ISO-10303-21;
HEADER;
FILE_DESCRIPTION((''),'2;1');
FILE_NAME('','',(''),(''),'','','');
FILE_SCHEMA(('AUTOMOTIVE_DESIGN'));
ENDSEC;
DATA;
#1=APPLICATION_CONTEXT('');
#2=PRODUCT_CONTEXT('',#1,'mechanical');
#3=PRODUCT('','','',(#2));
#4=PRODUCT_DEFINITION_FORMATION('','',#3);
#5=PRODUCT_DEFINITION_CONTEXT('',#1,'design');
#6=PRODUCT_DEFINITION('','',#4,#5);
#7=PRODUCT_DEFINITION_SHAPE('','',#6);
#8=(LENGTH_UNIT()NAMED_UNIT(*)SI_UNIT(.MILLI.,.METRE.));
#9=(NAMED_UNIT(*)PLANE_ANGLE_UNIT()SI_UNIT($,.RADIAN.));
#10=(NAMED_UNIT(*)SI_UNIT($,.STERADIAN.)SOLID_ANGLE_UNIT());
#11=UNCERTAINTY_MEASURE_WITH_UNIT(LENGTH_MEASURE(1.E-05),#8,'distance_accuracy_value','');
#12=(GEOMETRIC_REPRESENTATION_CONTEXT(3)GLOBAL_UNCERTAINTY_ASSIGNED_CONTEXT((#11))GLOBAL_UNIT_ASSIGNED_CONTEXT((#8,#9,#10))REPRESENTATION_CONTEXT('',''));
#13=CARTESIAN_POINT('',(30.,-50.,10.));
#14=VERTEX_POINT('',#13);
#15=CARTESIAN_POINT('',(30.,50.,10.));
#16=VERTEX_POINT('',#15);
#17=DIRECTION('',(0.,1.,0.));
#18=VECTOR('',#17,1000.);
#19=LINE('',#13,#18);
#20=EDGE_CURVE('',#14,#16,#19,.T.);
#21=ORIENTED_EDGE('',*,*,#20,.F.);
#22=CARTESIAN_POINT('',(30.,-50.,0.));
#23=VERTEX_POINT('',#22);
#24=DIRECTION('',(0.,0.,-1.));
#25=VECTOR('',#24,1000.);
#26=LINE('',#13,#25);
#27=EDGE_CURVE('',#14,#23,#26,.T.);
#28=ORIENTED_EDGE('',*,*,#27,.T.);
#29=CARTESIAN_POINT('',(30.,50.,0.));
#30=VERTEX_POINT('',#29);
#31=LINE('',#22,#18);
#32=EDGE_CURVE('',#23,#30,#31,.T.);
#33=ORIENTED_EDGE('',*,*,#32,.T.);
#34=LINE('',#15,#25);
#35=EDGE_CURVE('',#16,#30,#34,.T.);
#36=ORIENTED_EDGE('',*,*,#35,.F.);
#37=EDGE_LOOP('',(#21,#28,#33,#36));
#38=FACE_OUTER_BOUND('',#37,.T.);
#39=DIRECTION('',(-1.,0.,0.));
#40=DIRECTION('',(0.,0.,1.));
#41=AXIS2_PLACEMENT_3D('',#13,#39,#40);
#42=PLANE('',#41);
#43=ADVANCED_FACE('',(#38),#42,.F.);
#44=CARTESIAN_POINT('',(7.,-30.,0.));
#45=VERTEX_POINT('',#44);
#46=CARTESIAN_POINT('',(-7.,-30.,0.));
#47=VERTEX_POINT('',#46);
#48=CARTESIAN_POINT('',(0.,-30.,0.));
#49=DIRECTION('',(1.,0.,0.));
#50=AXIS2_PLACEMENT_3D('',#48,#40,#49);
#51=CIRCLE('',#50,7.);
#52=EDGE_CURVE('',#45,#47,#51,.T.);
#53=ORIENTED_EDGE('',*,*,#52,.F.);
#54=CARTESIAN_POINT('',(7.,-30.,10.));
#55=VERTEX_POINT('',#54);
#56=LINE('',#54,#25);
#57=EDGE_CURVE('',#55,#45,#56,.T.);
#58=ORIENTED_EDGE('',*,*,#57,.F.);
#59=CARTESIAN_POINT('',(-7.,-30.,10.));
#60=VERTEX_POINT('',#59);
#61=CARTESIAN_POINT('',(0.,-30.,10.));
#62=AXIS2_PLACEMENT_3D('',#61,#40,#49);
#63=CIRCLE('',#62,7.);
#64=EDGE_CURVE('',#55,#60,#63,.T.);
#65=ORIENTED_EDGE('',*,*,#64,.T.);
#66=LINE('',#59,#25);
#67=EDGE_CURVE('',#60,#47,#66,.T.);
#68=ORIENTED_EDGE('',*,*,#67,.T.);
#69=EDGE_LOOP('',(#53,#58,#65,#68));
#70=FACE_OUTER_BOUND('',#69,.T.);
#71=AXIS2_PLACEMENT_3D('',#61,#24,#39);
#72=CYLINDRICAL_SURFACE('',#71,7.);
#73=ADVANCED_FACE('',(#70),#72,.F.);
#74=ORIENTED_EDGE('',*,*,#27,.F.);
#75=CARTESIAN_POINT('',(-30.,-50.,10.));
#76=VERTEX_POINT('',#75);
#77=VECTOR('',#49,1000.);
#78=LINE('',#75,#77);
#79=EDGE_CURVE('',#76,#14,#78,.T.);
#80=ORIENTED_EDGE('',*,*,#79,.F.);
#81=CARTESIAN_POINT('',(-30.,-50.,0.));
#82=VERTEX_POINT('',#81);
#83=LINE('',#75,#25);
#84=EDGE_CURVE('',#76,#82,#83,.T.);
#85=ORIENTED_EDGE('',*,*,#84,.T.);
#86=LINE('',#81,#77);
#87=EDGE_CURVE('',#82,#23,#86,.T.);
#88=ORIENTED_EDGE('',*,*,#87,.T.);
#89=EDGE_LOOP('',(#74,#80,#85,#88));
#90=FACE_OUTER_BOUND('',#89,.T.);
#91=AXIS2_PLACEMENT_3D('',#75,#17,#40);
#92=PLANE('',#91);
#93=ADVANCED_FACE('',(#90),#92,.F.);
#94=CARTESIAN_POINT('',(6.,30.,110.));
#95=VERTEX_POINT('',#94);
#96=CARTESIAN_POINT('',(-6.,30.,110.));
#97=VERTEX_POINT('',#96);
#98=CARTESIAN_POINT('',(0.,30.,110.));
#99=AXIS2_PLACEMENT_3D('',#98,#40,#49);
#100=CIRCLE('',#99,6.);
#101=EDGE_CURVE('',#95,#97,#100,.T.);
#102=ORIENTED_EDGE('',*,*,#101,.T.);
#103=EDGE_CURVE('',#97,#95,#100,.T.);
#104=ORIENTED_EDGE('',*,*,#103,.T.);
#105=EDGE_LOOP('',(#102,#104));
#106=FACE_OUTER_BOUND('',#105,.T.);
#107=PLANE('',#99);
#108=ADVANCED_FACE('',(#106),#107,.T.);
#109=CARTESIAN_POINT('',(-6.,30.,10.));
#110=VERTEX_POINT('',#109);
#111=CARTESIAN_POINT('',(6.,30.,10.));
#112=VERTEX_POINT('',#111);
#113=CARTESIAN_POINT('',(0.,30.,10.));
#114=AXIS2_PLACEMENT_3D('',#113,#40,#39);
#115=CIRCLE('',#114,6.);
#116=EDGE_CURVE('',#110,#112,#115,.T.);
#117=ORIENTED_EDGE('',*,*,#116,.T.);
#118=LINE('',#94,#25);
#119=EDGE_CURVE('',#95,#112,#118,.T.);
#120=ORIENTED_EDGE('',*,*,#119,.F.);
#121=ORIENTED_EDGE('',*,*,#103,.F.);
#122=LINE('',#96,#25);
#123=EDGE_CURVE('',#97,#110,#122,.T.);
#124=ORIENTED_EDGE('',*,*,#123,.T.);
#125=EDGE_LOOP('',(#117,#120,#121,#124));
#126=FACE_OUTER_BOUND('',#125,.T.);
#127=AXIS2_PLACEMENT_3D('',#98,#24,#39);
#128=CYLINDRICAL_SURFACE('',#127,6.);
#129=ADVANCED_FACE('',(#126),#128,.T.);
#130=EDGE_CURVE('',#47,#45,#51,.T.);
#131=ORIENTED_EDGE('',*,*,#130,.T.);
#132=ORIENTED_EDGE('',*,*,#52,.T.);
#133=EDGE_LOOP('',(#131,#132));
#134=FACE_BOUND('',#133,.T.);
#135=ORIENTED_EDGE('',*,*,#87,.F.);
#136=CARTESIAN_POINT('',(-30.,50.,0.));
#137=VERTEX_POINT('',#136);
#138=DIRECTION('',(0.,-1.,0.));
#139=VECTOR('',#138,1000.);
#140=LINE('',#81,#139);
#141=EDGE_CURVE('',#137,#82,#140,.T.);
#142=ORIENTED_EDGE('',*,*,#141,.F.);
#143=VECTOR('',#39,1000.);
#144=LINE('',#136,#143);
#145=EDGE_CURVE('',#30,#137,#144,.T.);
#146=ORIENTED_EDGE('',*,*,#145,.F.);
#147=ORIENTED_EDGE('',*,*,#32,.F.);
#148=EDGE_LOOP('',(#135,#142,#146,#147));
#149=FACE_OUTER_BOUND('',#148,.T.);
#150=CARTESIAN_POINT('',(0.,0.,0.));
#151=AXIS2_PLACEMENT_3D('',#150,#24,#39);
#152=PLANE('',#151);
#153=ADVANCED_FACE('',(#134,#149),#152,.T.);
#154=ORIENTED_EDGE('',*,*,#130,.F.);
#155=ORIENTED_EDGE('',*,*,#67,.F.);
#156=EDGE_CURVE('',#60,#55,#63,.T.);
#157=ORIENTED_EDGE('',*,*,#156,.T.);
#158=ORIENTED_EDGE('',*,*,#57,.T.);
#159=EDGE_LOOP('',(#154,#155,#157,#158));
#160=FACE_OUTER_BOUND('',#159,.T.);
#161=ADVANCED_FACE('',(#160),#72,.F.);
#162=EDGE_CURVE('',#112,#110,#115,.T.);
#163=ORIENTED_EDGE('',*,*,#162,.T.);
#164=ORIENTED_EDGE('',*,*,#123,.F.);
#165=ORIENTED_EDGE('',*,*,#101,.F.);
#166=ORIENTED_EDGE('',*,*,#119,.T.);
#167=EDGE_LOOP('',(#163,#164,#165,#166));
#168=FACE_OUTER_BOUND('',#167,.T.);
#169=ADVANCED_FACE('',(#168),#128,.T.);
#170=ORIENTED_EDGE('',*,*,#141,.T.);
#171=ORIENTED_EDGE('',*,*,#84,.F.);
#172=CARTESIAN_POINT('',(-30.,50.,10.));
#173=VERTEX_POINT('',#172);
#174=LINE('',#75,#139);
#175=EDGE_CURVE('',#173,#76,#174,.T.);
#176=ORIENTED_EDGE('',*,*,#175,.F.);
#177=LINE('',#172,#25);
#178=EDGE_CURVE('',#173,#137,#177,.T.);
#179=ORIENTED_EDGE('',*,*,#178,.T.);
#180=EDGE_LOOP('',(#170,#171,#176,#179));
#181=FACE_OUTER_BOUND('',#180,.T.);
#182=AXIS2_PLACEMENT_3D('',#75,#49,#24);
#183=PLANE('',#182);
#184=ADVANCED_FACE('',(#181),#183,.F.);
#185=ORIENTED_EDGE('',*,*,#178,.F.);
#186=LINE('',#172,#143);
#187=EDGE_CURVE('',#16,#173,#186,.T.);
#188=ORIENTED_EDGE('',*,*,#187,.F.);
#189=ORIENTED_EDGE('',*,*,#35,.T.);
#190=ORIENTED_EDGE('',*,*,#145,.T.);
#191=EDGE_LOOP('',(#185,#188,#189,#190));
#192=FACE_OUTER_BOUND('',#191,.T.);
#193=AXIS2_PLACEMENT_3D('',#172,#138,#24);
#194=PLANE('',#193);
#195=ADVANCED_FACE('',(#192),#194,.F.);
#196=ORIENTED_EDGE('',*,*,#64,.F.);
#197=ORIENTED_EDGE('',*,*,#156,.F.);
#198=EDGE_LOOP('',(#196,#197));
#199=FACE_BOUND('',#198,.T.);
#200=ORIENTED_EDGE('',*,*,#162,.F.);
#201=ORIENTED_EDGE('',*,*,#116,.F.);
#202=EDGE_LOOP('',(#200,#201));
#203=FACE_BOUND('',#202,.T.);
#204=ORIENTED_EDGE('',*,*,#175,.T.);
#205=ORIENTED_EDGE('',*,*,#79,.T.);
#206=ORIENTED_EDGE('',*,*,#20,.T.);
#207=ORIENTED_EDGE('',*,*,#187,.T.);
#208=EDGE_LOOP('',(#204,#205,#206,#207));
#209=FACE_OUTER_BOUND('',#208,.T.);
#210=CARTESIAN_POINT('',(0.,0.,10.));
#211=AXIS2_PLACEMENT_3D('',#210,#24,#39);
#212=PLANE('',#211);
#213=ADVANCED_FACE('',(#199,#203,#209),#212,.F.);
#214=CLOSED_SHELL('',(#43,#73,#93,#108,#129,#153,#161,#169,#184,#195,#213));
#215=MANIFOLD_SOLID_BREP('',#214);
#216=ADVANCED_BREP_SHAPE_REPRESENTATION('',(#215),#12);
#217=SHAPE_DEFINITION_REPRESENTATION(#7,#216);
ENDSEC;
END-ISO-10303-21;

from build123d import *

# Parameters (mm, degrees)
SKETCH1_W           = 60
SKETCH1_H           = 100
SKETCH1_R           = 7
BOSS_EXTRUDE1_DEPTH = 10
SKETCH2_R           = 6
BOSS_EXTRUDE2_DEPTH = 100


with BuildPart() as part:
    # Sketch1 → Boss-Extrude1 (new body)
    with BuildSketch(Plane.XY):
        Rectangle(SKETCH1_W, SKETCH1_H)
        with Locations((0, -30)):
            Circle(SKETCH1_R, mode=Mode.SUBTRACT)
    extrude(amount=BOSS_EXTRUDE1_DEPTH)

    # Sketch2 → Boss-Extrude2 (add)
    with BuildSketch(Plane.XY.offset(10)):
        with Locations(Location((0, 30, 0), (0, 0, 180))):
            Circle(SKETCH2_R)
    extrude(amount=BOSS_EXTRUDE2_DEPTH)


solid = part.part
